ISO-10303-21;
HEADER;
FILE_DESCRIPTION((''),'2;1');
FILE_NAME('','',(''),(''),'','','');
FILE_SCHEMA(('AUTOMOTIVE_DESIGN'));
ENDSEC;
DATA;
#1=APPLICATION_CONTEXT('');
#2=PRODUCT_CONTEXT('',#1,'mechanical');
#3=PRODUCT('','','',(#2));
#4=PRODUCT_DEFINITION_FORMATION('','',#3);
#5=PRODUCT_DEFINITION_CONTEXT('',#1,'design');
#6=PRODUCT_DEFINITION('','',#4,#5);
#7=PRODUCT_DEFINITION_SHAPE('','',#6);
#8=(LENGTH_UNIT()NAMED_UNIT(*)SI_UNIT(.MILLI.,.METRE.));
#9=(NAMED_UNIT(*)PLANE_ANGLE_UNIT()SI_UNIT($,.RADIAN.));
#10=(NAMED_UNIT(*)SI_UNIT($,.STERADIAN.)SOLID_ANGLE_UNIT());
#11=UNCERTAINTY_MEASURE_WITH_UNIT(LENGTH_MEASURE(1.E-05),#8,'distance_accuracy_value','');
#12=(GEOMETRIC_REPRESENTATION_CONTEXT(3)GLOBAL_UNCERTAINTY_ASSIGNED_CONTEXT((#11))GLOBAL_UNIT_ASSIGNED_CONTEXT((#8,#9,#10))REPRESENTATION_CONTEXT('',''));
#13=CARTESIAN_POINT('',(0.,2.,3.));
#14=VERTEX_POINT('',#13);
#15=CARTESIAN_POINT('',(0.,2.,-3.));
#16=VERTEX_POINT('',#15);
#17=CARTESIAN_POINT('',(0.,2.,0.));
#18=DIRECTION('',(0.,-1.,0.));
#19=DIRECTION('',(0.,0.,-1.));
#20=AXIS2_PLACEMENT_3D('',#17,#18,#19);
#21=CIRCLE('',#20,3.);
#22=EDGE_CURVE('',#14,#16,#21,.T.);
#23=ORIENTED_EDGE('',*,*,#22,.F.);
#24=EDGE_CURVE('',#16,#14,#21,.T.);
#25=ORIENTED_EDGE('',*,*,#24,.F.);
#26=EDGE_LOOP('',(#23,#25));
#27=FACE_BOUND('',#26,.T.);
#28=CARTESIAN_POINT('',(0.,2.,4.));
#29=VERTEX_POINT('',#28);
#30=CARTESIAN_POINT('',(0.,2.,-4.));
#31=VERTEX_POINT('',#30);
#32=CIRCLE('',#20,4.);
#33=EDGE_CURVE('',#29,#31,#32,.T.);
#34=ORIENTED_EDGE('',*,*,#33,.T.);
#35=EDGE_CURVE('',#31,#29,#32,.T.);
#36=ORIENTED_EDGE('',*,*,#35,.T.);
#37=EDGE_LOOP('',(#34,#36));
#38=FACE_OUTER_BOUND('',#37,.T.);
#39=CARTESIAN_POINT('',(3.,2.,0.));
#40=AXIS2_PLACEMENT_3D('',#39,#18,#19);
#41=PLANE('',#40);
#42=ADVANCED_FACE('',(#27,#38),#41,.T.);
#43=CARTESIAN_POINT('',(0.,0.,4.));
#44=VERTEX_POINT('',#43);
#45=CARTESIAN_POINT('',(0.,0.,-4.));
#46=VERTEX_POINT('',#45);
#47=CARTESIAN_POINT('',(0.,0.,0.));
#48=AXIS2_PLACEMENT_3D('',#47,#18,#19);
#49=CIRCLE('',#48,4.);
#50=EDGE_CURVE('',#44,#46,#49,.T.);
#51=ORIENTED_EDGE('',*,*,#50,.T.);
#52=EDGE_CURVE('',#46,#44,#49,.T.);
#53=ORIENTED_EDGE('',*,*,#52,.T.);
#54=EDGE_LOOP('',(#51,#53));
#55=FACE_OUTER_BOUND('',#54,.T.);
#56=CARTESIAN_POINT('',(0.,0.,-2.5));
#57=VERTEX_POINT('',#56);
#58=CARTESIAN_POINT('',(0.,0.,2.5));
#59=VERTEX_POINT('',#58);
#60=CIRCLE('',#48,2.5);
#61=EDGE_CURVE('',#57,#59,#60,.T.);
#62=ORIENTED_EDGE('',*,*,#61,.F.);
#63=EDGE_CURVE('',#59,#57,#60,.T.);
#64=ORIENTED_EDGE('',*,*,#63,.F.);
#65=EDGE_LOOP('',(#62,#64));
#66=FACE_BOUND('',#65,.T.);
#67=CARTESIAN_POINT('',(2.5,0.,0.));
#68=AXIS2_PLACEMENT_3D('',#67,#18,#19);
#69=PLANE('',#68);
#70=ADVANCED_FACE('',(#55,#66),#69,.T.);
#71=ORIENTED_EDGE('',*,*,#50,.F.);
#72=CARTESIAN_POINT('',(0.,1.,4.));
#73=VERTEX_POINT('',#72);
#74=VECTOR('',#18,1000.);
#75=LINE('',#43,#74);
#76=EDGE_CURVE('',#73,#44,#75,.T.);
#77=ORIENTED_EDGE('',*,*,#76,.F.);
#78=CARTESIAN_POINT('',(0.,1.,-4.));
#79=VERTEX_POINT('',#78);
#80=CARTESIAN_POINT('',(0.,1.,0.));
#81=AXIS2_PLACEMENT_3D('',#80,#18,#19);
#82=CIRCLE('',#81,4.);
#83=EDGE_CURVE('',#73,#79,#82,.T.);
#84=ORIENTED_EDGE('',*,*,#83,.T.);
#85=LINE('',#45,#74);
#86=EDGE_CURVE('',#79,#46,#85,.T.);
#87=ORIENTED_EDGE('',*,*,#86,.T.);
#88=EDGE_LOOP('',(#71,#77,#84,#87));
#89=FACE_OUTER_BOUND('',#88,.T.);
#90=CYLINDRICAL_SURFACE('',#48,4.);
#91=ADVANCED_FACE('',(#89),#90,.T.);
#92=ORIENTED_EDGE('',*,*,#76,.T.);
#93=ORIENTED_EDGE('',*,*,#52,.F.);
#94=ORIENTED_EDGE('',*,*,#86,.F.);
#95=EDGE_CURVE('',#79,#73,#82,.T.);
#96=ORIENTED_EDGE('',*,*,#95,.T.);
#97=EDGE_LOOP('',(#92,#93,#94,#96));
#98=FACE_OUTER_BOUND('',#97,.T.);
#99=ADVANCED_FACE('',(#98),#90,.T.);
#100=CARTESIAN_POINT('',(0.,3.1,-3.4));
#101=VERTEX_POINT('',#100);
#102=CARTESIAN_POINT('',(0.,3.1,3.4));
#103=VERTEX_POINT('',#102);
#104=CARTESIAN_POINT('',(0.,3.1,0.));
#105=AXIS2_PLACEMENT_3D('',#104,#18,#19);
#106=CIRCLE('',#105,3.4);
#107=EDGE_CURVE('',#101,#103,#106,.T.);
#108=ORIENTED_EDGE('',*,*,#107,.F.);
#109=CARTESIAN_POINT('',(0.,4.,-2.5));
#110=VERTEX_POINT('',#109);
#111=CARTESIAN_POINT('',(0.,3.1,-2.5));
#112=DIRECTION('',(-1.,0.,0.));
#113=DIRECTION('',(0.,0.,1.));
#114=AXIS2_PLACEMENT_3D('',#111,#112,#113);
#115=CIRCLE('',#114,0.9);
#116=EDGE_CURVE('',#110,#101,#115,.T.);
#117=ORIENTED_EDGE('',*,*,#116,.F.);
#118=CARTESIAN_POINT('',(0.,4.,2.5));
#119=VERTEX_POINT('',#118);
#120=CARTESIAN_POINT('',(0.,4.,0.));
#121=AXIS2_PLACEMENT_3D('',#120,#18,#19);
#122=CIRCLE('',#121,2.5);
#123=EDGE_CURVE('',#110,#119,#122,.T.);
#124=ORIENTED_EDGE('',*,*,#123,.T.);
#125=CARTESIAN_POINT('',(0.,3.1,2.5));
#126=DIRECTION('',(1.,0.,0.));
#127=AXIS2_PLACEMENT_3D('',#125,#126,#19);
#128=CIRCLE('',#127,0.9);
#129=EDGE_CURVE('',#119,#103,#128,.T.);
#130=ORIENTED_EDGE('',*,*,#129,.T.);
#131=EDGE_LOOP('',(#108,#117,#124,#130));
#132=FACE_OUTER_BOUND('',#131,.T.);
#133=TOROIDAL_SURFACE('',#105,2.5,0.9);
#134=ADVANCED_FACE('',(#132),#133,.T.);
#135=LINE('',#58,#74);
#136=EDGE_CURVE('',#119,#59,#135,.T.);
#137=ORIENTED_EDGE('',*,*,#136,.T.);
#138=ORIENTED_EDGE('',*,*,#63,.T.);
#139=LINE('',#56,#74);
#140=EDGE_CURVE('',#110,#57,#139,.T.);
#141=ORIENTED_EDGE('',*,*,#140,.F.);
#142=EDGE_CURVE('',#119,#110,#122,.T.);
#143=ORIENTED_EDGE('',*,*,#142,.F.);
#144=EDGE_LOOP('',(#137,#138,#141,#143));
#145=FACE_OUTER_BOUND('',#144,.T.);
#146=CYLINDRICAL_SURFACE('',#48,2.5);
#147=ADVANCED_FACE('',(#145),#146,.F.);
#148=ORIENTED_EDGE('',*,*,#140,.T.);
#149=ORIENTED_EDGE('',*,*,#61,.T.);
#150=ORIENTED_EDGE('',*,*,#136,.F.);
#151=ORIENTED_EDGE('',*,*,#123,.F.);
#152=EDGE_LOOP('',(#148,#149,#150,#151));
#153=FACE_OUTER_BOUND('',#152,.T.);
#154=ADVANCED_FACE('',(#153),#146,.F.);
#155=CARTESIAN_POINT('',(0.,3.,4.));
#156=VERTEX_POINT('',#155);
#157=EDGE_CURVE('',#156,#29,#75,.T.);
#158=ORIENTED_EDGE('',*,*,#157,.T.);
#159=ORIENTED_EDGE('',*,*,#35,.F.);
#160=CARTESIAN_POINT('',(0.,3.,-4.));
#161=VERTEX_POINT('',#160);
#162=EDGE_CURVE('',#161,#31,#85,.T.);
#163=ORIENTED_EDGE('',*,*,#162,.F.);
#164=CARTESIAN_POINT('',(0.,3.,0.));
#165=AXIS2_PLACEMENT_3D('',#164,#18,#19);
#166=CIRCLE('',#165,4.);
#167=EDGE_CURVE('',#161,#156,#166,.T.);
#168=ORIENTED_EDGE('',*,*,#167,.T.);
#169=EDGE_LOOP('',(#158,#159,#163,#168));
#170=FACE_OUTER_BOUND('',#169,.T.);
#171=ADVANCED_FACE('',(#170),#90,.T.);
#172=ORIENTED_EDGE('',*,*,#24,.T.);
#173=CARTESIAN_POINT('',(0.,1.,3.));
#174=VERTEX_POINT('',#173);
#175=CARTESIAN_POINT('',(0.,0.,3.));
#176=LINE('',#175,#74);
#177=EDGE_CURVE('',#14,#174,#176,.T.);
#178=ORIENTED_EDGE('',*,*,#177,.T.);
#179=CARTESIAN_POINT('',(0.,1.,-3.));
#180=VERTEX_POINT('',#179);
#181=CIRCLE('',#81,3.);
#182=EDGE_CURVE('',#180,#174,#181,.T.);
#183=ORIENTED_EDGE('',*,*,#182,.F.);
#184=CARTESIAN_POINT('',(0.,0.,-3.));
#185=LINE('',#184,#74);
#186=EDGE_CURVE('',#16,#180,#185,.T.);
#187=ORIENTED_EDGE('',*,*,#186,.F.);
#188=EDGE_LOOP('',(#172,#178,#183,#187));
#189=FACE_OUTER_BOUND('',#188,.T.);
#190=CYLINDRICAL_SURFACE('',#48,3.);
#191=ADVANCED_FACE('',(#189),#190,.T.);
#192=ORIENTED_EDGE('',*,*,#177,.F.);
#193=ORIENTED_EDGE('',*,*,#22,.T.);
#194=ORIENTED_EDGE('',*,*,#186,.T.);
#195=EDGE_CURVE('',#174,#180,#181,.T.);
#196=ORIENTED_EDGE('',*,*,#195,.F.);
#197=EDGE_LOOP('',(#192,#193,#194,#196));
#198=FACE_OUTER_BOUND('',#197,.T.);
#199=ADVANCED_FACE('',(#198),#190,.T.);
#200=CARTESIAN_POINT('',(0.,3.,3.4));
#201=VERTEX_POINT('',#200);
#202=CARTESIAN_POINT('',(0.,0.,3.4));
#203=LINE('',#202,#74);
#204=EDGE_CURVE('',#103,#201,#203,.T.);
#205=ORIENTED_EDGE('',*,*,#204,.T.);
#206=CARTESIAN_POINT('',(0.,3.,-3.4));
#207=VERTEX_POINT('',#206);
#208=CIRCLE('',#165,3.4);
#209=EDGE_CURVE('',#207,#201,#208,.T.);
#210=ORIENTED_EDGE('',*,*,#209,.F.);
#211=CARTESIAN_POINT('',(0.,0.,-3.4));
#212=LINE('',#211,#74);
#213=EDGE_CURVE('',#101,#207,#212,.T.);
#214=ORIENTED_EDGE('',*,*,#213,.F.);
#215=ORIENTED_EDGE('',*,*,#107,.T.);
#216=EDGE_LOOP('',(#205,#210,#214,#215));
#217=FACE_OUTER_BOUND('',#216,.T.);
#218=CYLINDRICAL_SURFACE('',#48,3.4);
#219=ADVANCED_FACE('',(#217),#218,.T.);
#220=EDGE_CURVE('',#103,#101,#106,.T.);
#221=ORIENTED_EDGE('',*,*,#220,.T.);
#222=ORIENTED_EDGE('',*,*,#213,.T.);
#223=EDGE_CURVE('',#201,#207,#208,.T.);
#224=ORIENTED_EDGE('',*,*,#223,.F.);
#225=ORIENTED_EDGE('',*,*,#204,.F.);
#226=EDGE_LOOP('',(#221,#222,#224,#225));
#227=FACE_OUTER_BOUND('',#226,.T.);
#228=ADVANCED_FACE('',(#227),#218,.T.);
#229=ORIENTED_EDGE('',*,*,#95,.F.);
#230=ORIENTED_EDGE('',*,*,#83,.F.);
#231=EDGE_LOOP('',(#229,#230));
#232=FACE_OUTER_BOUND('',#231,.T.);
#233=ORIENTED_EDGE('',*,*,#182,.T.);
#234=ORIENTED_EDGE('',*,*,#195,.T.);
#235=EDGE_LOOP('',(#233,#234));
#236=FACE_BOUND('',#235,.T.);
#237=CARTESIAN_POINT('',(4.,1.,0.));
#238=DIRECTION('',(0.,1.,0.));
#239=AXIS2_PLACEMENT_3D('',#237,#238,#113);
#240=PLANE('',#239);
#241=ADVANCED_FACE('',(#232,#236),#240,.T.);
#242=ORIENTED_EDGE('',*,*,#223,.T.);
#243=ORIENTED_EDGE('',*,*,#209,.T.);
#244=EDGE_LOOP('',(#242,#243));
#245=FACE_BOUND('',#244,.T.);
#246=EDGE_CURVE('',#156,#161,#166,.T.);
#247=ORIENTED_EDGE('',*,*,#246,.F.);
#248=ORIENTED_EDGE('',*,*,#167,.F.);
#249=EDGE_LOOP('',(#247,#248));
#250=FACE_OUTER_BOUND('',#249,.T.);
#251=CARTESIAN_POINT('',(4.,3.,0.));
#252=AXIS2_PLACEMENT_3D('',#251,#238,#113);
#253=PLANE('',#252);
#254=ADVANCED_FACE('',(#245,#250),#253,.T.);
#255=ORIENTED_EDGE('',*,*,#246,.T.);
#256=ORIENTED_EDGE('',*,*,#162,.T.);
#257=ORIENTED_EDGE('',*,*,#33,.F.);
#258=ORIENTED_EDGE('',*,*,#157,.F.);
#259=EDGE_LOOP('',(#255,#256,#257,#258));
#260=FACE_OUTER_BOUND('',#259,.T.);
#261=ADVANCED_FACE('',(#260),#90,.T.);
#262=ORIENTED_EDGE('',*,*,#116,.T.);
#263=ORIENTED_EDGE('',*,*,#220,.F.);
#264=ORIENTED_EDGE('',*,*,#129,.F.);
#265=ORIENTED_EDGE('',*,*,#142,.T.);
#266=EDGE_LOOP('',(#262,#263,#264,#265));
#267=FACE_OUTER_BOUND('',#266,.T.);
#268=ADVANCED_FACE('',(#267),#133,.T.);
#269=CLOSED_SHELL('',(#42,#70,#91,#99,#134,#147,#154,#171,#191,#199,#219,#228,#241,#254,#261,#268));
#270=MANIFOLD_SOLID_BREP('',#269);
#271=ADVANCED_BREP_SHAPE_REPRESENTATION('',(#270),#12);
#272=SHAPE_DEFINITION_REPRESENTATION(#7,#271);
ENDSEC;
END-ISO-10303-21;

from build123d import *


with BuildPart() as part:
    # 草图1 → 旋转1 (revolve)
    with BuildSketch(Plane.XY, mode=Mode.PRIVATE) as revolve_1_sk:
        with BuildLine():
            Line((2.5, 0), (4, 0))
            Line((4, 0), (4, 1))
            Line((4, 1), (3, 1))
            Line((3, 1), (3, 2))
            Line((3, 2), (4, 2))
            Line((4, 2), (4, 3))
            Line((4, 3), (3.4, 3))
            Line((3.4, 3), (3.4, 3.1))
            ThreePointArc((3.4, 3.1), (3.136396103, 3.736396103), (2.5, 4))
            Line((2.5, 4), (2.5, 0))
        make_face()
    revolve(revolve_1_sk.sketch.rotate(Axis((0, 0, 0), (0, 1, 0)), 90), axis=Axis((0, 0, 0), (0, 1, 0)))


solid = part.part
